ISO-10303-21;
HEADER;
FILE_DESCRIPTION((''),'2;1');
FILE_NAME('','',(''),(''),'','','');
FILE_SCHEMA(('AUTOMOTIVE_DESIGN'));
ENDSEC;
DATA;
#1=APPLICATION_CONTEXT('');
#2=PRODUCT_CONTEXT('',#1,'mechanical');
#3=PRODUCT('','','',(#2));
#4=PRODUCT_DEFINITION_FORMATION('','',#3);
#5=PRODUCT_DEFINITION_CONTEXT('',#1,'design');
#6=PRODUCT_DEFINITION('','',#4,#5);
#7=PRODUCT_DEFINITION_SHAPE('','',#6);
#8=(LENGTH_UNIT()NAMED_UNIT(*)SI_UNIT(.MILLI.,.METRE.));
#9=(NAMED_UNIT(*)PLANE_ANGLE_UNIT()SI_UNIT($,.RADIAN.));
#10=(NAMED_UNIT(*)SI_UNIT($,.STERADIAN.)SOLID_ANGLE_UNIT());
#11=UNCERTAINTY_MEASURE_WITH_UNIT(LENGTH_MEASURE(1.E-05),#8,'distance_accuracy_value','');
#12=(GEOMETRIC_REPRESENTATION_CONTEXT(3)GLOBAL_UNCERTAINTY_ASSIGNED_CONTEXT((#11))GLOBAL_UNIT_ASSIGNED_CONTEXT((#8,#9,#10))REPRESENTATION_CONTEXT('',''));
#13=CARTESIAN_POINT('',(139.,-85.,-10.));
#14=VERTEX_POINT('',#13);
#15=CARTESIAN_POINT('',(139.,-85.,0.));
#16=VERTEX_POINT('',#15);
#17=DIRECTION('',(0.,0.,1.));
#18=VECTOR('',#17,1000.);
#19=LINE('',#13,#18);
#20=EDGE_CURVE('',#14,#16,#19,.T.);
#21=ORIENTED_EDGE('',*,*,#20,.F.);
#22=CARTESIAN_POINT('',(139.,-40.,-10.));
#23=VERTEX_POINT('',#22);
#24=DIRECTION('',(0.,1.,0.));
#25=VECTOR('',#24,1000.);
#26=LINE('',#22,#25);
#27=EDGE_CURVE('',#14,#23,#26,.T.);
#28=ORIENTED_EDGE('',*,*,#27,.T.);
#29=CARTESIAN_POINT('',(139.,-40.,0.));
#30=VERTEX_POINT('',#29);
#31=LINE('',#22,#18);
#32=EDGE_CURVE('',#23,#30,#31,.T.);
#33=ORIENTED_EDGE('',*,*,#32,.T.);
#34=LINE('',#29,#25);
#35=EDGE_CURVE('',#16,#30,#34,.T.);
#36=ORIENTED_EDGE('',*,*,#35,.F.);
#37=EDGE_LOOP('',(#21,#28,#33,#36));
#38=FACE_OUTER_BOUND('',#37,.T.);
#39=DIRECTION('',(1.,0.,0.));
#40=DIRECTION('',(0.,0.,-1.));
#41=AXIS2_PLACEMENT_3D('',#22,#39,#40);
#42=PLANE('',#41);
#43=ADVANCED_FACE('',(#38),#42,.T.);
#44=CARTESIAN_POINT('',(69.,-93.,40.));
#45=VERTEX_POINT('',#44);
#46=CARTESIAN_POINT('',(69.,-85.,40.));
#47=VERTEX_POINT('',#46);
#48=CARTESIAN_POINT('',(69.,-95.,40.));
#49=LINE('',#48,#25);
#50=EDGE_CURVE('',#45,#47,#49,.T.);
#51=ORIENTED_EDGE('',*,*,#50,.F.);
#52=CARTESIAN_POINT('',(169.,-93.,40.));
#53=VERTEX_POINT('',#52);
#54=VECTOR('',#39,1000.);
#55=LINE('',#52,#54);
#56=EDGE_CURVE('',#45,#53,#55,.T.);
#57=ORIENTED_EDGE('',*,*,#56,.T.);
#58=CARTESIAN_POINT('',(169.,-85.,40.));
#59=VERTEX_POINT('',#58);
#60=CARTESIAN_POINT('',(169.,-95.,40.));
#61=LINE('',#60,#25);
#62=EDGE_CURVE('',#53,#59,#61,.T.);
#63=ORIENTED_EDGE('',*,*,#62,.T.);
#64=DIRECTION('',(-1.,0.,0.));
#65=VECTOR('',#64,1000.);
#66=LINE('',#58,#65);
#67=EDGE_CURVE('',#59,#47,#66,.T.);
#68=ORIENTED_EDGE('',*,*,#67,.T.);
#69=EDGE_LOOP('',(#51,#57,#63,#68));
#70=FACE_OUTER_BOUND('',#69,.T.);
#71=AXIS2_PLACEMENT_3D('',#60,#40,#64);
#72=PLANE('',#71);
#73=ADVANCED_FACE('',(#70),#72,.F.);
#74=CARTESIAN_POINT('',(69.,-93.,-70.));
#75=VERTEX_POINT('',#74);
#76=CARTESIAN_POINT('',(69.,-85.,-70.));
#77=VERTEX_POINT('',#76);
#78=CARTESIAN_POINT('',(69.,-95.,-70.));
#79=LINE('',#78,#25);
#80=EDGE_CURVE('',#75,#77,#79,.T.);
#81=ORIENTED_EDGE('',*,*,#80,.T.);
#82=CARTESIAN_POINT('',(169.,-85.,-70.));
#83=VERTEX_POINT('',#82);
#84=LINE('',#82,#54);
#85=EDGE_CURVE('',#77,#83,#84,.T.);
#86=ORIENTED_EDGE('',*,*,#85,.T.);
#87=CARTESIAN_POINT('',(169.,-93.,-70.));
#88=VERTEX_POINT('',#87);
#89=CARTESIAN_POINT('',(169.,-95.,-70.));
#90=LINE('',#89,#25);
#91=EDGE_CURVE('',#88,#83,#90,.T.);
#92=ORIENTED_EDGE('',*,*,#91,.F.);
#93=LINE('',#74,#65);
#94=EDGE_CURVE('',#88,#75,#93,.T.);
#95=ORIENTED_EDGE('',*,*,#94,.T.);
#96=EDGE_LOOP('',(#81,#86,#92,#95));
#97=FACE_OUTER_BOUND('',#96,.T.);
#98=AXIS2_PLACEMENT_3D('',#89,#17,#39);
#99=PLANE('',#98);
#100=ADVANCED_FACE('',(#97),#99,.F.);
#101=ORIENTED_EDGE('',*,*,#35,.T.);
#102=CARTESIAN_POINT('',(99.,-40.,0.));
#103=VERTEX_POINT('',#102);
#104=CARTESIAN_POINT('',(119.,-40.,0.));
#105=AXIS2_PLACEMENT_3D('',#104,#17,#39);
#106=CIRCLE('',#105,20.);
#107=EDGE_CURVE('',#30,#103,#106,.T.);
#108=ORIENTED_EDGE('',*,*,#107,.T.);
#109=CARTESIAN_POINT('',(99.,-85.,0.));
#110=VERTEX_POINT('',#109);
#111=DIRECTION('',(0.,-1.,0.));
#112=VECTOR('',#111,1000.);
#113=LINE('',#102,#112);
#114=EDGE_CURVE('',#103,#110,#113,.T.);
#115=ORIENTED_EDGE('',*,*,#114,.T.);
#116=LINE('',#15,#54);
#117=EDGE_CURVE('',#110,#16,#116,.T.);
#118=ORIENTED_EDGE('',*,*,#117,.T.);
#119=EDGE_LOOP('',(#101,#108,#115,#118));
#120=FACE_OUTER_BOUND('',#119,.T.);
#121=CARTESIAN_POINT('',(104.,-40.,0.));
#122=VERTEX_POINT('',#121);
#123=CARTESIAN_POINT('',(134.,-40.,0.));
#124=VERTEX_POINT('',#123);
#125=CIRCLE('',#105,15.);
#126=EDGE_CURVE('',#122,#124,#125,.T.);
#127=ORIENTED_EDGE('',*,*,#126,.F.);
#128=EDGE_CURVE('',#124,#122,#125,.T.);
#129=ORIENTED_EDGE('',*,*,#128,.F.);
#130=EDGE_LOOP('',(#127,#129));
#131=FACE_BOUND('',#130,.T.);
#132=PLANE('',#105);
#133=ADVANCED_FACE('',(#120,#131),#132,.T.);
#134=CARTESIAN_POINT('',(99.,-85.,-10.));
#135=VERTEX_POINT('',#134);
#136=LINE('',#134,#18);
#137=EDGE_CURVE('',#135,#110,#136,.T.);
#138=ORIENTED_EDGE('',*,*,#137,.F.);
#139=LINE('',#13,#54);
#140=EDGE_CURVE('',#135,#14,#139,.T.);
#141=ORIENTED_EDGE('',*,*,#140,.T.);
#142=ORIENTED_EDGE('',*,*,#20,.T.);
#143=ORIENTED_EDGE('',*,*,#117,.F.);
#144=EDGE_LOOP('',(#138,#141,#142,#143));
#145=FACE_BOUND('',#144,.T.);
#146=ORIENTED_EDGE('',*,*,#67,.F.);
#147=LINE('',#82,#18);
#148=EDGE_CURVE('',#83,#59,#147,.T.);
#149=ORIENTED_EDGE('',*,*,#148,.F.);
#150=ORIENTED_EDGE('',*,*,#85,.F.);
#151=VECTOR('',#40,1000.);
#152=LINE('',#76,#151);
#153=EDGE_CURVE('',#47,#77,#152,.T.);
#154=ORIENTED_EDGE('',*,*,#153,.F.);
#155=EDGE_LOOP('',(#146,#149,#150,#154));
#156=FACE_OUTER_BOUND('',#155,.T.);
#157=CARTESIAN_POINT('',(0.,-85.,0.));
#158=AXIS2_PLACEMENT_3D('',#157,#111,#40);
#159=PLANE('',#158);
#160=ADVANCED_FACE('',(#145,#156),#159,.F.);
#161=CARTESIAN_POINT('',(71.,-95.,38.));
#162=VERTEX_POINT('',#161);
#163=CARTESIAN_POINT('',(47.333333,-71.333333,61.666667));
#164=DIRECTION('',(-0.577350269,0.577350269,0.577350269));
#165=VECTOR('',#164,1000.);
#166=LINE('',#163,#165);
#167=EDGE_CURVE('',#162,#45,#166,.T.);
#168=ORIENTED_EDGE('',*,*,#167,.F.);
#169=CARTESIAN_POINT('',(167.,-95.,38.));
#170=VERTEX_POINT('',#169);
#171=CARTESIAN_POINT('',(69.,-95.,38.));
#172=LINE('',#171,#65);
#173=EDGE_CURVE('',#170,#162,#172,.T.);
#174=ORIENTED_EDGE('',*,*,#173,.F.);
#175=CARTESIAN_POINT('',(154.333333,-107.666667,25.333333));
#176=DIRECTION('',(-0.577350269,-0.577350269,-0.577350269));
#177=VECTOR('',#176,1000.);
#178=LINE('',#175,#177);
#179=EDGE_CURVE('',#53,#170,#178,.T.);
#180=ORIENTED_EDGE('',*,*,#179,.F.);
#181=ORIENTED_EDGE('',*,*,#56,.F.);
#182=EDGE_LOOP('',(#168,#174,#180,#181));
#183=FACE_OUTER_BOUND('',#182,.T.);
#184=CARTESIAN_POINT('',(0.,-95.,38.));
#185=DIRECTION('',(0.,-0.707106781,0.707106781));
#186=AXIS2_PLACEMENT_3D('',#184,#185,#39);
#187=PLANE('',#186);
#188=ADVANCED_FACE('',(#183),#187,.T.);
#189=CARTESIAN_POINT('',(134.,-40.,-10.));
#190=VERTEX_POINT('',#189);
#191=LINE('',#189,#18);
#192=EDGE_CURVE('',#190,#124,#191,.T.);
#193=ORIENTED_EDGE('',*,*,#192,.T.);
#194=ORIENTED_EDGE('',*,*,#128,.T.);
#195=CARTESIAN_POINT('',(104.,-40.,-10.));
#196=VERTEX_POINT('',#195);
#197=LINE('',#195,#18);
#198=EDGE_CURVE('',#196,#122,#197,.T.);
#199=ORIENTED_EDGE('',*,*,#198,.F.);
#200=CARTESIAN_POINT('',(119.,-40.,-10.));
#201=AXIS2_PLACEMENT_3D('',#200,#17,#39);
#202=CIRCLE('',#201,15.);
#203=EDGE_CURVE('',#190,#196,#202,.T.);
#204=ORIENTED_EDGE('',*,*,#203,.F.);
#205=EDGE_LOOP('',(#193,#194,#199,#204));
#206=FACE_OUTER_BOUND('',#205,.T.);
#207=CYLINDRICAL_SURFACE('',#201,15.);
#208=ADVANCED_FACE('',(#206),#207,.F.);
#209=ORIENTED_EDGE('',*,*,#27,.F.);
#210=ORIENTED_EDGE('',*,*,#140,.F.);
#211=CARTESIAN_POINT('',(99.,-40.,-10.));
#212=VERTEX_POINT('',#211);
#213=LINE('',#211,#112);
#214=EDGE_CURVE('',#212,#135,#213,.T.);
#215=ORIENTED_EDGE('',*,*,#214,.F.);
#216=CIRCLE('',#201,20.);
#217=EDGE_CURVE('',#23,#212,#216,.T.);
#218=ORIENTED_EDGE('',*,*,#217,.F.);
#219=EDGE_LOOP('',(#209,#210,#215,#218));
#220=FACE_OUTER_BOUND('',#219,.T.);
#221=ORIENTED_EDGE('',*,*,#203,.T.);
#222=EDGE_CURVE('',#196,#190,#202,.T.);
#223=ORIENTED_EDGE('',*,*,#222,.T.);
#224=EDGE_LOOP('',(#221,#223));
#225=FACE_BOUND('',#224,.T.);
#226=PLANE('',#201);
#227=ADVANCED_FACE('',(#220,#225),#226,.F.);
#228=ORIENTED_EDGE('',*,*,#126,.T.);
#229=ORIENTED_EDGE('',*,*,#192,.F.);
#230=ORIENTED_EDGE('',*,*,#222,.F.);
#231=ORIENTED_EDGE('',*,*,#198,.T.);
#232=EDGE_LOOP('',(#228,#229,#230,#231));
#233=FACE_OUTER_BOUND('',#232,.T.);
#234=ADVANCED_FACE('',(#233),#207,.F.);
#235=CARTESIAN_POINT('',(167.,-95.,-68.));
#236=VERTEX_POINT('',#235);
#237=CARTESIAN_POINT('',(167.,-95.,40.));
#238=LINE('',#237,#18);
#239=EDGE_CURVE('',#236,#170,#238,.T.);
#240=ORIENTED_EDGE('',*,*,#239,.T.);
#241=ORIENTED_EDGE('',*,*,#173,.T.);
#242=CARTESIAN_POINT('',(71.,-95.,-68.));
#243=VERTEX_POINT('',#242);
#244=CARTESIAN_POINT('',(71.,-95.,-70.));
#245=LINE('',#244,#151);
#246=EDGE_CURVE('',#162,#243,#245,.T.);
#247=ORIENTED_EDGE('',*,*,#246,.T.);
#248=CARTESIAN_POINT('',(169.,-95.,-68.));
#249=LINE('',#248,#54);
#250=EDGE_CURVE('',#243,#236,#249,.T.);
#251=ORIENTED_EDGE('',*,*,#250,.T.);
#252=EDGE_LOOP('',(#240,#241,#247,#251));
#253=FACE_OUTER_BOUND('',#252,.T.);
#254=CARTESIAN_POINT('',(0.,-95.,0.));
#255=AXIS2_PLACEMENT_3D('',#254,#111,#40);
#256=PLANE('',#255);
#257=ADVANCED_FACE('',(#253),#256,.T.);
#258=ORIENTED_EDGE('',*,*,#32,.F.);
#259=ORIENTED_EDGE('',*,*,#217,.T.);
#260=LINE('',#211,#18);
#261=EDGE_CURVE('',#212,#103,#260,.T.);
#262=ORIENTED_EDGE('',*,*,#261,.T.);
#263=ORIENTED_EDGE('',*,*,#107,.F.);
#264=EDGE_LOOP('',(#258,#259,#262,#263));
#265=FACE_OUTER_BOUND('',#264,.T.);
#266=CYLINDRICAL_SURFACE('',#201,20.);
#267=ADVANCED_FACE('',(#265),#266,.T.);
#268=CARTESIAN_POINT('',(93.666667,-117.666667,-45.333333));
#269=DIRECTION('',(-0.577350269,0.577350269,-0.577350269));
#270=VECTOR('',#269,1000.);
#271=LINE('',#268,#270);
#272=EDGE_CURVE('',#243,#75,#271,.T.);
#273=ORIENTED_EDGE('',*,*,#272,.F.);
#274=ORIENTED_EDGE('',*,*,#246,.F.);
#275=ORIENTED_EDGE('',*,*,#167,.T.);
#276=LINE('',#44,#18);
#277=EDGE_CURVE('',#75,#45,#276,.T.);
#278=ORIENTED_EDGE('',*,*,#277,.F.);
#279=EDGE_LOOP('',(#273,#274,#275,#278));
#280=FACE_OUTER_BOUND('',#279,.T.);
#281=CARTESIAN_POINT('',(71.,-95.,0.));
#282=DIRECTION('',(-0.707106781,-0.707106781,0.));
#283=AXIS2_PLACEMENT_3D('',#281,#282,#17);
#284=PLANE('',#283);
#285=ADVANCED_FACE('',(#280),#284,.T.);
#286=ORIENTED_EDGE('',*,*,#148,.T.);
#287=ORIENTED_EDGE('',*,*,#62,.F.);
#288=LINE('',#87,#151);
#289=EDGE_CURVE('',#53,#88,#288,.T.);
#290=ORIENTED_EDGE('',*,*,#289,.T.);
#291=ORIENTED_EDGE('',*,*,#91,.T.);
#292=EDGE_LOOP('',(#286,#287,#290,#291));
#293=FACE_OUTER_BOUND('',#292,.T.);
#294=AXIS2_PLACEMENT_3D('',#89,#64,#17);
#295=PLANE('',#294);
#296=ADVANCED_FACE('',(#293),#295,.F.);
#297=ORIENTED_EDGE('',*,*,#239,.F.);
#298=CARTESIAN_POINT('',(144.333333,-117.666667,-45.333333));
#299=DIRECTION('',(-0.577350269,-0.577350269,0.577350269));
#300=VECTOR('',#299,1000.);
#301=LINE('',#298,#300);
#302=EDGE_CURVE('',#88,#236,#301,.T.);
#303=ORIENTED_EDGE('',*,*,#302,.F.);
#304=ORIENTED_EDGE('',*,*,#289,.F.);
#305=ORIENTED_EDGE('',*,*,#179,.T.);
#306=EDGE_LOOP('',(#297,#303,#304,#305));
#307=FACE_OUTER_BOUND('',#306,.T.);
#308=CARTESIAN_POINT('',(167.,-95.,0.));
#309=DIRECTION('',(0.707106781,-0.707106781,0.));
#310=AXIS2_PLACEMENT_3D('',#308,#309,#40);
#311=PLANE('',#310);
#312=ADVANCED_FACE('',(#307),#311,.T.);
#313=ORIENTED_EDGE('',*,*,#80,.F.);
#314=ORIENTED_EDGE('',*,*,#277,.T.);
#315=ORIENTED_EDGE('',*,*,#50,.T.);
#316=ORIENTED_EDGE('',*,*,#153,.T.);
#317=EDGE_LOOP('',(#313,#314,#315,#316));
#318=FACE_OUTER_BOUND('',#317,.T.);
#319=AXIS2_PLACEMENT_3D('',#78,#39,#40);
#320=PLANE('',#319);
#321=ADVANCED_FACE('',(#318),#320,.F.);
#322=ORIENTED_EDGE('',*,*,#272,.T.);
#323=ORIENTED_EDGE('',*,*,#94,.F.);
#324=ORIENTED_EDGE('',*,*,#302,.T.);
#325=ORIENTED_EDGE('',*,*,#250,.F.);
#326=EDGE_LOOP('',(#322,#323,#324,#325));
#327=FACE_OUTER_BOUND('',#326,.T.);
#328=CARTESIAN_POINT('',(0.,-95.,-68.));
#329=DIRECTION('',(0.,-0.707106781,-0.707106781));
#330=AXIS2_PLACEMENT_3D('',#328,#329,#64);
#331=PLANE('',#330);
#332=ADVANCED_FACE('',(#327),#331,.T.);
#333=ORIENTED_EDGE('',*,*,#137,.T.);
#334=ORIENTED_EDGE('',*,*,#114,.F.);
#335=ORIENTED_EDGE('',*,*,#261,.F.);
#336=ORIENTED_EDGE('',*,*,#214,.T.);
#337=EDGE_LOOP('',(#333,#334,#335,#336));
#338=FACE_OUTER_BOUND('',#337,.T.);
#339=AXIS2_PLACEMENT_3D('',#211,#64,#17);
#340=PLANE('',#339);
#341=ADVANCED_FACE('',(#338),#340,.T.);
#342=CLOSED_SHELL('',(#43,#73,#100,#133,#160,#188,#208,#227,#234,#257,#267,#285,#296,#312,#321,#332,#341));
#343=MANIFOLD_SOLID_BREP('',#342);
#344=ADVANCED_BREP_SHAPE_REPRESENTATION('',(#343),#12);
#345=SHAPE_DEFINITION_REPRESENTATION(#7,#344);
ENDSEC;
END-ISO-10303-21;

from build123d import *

# Parameters (mm, degrees)
SKETCH1_R           = 15
BOSS_EXTRUDE1_DEPTH = 10
SKETCH2_W           = 100
SKETCH2_H           = 110
BOSS_EXTRUDE2_DEPTH = 10
CHAMFER1_SIZE       = 2


with BuildPart() as part:
    # Sketch1 → Boss-Extrude1 (new body)
    with BuildSketch(Plane.XY):
        with BuildLine():
            Line((139, -40), (139, -85))
            Line((139, -85), (99, -85))
            Line((99, -85), (99, -40))
            ThreePointArc((99, -40), (119, -20), (139, -40))
        make_face()
        with Locations((119, -40)):
            Circle(SKETCH1_R, mode=Mode.SUBTRACT)
    extrude(amount=-BOSS_EXTRUDE1_DEPTH)

    # Sketch2 → Boss-Extrude2 (add)
    with BuildSketch(Plane.XZ.offset(85)):
        with Locations((119, -15)):
            Rectangle(SKETCH2_W, SKETCH2_H)
    extrude(amount=BOSS_EXTRUDE2_DEPTH)

    # Chamfer1
    chamfer1_edges = [part.edges().sort_by_distance(p)[0] for p in [
        (169, -95, -15),
        (119, -95, 40),
        (69, -95, -15),
        (119, -95, -70),
    ]]
    chamfer(chamfer1_edges, length=CHAMFER1_SIZE)


solid = part.part
